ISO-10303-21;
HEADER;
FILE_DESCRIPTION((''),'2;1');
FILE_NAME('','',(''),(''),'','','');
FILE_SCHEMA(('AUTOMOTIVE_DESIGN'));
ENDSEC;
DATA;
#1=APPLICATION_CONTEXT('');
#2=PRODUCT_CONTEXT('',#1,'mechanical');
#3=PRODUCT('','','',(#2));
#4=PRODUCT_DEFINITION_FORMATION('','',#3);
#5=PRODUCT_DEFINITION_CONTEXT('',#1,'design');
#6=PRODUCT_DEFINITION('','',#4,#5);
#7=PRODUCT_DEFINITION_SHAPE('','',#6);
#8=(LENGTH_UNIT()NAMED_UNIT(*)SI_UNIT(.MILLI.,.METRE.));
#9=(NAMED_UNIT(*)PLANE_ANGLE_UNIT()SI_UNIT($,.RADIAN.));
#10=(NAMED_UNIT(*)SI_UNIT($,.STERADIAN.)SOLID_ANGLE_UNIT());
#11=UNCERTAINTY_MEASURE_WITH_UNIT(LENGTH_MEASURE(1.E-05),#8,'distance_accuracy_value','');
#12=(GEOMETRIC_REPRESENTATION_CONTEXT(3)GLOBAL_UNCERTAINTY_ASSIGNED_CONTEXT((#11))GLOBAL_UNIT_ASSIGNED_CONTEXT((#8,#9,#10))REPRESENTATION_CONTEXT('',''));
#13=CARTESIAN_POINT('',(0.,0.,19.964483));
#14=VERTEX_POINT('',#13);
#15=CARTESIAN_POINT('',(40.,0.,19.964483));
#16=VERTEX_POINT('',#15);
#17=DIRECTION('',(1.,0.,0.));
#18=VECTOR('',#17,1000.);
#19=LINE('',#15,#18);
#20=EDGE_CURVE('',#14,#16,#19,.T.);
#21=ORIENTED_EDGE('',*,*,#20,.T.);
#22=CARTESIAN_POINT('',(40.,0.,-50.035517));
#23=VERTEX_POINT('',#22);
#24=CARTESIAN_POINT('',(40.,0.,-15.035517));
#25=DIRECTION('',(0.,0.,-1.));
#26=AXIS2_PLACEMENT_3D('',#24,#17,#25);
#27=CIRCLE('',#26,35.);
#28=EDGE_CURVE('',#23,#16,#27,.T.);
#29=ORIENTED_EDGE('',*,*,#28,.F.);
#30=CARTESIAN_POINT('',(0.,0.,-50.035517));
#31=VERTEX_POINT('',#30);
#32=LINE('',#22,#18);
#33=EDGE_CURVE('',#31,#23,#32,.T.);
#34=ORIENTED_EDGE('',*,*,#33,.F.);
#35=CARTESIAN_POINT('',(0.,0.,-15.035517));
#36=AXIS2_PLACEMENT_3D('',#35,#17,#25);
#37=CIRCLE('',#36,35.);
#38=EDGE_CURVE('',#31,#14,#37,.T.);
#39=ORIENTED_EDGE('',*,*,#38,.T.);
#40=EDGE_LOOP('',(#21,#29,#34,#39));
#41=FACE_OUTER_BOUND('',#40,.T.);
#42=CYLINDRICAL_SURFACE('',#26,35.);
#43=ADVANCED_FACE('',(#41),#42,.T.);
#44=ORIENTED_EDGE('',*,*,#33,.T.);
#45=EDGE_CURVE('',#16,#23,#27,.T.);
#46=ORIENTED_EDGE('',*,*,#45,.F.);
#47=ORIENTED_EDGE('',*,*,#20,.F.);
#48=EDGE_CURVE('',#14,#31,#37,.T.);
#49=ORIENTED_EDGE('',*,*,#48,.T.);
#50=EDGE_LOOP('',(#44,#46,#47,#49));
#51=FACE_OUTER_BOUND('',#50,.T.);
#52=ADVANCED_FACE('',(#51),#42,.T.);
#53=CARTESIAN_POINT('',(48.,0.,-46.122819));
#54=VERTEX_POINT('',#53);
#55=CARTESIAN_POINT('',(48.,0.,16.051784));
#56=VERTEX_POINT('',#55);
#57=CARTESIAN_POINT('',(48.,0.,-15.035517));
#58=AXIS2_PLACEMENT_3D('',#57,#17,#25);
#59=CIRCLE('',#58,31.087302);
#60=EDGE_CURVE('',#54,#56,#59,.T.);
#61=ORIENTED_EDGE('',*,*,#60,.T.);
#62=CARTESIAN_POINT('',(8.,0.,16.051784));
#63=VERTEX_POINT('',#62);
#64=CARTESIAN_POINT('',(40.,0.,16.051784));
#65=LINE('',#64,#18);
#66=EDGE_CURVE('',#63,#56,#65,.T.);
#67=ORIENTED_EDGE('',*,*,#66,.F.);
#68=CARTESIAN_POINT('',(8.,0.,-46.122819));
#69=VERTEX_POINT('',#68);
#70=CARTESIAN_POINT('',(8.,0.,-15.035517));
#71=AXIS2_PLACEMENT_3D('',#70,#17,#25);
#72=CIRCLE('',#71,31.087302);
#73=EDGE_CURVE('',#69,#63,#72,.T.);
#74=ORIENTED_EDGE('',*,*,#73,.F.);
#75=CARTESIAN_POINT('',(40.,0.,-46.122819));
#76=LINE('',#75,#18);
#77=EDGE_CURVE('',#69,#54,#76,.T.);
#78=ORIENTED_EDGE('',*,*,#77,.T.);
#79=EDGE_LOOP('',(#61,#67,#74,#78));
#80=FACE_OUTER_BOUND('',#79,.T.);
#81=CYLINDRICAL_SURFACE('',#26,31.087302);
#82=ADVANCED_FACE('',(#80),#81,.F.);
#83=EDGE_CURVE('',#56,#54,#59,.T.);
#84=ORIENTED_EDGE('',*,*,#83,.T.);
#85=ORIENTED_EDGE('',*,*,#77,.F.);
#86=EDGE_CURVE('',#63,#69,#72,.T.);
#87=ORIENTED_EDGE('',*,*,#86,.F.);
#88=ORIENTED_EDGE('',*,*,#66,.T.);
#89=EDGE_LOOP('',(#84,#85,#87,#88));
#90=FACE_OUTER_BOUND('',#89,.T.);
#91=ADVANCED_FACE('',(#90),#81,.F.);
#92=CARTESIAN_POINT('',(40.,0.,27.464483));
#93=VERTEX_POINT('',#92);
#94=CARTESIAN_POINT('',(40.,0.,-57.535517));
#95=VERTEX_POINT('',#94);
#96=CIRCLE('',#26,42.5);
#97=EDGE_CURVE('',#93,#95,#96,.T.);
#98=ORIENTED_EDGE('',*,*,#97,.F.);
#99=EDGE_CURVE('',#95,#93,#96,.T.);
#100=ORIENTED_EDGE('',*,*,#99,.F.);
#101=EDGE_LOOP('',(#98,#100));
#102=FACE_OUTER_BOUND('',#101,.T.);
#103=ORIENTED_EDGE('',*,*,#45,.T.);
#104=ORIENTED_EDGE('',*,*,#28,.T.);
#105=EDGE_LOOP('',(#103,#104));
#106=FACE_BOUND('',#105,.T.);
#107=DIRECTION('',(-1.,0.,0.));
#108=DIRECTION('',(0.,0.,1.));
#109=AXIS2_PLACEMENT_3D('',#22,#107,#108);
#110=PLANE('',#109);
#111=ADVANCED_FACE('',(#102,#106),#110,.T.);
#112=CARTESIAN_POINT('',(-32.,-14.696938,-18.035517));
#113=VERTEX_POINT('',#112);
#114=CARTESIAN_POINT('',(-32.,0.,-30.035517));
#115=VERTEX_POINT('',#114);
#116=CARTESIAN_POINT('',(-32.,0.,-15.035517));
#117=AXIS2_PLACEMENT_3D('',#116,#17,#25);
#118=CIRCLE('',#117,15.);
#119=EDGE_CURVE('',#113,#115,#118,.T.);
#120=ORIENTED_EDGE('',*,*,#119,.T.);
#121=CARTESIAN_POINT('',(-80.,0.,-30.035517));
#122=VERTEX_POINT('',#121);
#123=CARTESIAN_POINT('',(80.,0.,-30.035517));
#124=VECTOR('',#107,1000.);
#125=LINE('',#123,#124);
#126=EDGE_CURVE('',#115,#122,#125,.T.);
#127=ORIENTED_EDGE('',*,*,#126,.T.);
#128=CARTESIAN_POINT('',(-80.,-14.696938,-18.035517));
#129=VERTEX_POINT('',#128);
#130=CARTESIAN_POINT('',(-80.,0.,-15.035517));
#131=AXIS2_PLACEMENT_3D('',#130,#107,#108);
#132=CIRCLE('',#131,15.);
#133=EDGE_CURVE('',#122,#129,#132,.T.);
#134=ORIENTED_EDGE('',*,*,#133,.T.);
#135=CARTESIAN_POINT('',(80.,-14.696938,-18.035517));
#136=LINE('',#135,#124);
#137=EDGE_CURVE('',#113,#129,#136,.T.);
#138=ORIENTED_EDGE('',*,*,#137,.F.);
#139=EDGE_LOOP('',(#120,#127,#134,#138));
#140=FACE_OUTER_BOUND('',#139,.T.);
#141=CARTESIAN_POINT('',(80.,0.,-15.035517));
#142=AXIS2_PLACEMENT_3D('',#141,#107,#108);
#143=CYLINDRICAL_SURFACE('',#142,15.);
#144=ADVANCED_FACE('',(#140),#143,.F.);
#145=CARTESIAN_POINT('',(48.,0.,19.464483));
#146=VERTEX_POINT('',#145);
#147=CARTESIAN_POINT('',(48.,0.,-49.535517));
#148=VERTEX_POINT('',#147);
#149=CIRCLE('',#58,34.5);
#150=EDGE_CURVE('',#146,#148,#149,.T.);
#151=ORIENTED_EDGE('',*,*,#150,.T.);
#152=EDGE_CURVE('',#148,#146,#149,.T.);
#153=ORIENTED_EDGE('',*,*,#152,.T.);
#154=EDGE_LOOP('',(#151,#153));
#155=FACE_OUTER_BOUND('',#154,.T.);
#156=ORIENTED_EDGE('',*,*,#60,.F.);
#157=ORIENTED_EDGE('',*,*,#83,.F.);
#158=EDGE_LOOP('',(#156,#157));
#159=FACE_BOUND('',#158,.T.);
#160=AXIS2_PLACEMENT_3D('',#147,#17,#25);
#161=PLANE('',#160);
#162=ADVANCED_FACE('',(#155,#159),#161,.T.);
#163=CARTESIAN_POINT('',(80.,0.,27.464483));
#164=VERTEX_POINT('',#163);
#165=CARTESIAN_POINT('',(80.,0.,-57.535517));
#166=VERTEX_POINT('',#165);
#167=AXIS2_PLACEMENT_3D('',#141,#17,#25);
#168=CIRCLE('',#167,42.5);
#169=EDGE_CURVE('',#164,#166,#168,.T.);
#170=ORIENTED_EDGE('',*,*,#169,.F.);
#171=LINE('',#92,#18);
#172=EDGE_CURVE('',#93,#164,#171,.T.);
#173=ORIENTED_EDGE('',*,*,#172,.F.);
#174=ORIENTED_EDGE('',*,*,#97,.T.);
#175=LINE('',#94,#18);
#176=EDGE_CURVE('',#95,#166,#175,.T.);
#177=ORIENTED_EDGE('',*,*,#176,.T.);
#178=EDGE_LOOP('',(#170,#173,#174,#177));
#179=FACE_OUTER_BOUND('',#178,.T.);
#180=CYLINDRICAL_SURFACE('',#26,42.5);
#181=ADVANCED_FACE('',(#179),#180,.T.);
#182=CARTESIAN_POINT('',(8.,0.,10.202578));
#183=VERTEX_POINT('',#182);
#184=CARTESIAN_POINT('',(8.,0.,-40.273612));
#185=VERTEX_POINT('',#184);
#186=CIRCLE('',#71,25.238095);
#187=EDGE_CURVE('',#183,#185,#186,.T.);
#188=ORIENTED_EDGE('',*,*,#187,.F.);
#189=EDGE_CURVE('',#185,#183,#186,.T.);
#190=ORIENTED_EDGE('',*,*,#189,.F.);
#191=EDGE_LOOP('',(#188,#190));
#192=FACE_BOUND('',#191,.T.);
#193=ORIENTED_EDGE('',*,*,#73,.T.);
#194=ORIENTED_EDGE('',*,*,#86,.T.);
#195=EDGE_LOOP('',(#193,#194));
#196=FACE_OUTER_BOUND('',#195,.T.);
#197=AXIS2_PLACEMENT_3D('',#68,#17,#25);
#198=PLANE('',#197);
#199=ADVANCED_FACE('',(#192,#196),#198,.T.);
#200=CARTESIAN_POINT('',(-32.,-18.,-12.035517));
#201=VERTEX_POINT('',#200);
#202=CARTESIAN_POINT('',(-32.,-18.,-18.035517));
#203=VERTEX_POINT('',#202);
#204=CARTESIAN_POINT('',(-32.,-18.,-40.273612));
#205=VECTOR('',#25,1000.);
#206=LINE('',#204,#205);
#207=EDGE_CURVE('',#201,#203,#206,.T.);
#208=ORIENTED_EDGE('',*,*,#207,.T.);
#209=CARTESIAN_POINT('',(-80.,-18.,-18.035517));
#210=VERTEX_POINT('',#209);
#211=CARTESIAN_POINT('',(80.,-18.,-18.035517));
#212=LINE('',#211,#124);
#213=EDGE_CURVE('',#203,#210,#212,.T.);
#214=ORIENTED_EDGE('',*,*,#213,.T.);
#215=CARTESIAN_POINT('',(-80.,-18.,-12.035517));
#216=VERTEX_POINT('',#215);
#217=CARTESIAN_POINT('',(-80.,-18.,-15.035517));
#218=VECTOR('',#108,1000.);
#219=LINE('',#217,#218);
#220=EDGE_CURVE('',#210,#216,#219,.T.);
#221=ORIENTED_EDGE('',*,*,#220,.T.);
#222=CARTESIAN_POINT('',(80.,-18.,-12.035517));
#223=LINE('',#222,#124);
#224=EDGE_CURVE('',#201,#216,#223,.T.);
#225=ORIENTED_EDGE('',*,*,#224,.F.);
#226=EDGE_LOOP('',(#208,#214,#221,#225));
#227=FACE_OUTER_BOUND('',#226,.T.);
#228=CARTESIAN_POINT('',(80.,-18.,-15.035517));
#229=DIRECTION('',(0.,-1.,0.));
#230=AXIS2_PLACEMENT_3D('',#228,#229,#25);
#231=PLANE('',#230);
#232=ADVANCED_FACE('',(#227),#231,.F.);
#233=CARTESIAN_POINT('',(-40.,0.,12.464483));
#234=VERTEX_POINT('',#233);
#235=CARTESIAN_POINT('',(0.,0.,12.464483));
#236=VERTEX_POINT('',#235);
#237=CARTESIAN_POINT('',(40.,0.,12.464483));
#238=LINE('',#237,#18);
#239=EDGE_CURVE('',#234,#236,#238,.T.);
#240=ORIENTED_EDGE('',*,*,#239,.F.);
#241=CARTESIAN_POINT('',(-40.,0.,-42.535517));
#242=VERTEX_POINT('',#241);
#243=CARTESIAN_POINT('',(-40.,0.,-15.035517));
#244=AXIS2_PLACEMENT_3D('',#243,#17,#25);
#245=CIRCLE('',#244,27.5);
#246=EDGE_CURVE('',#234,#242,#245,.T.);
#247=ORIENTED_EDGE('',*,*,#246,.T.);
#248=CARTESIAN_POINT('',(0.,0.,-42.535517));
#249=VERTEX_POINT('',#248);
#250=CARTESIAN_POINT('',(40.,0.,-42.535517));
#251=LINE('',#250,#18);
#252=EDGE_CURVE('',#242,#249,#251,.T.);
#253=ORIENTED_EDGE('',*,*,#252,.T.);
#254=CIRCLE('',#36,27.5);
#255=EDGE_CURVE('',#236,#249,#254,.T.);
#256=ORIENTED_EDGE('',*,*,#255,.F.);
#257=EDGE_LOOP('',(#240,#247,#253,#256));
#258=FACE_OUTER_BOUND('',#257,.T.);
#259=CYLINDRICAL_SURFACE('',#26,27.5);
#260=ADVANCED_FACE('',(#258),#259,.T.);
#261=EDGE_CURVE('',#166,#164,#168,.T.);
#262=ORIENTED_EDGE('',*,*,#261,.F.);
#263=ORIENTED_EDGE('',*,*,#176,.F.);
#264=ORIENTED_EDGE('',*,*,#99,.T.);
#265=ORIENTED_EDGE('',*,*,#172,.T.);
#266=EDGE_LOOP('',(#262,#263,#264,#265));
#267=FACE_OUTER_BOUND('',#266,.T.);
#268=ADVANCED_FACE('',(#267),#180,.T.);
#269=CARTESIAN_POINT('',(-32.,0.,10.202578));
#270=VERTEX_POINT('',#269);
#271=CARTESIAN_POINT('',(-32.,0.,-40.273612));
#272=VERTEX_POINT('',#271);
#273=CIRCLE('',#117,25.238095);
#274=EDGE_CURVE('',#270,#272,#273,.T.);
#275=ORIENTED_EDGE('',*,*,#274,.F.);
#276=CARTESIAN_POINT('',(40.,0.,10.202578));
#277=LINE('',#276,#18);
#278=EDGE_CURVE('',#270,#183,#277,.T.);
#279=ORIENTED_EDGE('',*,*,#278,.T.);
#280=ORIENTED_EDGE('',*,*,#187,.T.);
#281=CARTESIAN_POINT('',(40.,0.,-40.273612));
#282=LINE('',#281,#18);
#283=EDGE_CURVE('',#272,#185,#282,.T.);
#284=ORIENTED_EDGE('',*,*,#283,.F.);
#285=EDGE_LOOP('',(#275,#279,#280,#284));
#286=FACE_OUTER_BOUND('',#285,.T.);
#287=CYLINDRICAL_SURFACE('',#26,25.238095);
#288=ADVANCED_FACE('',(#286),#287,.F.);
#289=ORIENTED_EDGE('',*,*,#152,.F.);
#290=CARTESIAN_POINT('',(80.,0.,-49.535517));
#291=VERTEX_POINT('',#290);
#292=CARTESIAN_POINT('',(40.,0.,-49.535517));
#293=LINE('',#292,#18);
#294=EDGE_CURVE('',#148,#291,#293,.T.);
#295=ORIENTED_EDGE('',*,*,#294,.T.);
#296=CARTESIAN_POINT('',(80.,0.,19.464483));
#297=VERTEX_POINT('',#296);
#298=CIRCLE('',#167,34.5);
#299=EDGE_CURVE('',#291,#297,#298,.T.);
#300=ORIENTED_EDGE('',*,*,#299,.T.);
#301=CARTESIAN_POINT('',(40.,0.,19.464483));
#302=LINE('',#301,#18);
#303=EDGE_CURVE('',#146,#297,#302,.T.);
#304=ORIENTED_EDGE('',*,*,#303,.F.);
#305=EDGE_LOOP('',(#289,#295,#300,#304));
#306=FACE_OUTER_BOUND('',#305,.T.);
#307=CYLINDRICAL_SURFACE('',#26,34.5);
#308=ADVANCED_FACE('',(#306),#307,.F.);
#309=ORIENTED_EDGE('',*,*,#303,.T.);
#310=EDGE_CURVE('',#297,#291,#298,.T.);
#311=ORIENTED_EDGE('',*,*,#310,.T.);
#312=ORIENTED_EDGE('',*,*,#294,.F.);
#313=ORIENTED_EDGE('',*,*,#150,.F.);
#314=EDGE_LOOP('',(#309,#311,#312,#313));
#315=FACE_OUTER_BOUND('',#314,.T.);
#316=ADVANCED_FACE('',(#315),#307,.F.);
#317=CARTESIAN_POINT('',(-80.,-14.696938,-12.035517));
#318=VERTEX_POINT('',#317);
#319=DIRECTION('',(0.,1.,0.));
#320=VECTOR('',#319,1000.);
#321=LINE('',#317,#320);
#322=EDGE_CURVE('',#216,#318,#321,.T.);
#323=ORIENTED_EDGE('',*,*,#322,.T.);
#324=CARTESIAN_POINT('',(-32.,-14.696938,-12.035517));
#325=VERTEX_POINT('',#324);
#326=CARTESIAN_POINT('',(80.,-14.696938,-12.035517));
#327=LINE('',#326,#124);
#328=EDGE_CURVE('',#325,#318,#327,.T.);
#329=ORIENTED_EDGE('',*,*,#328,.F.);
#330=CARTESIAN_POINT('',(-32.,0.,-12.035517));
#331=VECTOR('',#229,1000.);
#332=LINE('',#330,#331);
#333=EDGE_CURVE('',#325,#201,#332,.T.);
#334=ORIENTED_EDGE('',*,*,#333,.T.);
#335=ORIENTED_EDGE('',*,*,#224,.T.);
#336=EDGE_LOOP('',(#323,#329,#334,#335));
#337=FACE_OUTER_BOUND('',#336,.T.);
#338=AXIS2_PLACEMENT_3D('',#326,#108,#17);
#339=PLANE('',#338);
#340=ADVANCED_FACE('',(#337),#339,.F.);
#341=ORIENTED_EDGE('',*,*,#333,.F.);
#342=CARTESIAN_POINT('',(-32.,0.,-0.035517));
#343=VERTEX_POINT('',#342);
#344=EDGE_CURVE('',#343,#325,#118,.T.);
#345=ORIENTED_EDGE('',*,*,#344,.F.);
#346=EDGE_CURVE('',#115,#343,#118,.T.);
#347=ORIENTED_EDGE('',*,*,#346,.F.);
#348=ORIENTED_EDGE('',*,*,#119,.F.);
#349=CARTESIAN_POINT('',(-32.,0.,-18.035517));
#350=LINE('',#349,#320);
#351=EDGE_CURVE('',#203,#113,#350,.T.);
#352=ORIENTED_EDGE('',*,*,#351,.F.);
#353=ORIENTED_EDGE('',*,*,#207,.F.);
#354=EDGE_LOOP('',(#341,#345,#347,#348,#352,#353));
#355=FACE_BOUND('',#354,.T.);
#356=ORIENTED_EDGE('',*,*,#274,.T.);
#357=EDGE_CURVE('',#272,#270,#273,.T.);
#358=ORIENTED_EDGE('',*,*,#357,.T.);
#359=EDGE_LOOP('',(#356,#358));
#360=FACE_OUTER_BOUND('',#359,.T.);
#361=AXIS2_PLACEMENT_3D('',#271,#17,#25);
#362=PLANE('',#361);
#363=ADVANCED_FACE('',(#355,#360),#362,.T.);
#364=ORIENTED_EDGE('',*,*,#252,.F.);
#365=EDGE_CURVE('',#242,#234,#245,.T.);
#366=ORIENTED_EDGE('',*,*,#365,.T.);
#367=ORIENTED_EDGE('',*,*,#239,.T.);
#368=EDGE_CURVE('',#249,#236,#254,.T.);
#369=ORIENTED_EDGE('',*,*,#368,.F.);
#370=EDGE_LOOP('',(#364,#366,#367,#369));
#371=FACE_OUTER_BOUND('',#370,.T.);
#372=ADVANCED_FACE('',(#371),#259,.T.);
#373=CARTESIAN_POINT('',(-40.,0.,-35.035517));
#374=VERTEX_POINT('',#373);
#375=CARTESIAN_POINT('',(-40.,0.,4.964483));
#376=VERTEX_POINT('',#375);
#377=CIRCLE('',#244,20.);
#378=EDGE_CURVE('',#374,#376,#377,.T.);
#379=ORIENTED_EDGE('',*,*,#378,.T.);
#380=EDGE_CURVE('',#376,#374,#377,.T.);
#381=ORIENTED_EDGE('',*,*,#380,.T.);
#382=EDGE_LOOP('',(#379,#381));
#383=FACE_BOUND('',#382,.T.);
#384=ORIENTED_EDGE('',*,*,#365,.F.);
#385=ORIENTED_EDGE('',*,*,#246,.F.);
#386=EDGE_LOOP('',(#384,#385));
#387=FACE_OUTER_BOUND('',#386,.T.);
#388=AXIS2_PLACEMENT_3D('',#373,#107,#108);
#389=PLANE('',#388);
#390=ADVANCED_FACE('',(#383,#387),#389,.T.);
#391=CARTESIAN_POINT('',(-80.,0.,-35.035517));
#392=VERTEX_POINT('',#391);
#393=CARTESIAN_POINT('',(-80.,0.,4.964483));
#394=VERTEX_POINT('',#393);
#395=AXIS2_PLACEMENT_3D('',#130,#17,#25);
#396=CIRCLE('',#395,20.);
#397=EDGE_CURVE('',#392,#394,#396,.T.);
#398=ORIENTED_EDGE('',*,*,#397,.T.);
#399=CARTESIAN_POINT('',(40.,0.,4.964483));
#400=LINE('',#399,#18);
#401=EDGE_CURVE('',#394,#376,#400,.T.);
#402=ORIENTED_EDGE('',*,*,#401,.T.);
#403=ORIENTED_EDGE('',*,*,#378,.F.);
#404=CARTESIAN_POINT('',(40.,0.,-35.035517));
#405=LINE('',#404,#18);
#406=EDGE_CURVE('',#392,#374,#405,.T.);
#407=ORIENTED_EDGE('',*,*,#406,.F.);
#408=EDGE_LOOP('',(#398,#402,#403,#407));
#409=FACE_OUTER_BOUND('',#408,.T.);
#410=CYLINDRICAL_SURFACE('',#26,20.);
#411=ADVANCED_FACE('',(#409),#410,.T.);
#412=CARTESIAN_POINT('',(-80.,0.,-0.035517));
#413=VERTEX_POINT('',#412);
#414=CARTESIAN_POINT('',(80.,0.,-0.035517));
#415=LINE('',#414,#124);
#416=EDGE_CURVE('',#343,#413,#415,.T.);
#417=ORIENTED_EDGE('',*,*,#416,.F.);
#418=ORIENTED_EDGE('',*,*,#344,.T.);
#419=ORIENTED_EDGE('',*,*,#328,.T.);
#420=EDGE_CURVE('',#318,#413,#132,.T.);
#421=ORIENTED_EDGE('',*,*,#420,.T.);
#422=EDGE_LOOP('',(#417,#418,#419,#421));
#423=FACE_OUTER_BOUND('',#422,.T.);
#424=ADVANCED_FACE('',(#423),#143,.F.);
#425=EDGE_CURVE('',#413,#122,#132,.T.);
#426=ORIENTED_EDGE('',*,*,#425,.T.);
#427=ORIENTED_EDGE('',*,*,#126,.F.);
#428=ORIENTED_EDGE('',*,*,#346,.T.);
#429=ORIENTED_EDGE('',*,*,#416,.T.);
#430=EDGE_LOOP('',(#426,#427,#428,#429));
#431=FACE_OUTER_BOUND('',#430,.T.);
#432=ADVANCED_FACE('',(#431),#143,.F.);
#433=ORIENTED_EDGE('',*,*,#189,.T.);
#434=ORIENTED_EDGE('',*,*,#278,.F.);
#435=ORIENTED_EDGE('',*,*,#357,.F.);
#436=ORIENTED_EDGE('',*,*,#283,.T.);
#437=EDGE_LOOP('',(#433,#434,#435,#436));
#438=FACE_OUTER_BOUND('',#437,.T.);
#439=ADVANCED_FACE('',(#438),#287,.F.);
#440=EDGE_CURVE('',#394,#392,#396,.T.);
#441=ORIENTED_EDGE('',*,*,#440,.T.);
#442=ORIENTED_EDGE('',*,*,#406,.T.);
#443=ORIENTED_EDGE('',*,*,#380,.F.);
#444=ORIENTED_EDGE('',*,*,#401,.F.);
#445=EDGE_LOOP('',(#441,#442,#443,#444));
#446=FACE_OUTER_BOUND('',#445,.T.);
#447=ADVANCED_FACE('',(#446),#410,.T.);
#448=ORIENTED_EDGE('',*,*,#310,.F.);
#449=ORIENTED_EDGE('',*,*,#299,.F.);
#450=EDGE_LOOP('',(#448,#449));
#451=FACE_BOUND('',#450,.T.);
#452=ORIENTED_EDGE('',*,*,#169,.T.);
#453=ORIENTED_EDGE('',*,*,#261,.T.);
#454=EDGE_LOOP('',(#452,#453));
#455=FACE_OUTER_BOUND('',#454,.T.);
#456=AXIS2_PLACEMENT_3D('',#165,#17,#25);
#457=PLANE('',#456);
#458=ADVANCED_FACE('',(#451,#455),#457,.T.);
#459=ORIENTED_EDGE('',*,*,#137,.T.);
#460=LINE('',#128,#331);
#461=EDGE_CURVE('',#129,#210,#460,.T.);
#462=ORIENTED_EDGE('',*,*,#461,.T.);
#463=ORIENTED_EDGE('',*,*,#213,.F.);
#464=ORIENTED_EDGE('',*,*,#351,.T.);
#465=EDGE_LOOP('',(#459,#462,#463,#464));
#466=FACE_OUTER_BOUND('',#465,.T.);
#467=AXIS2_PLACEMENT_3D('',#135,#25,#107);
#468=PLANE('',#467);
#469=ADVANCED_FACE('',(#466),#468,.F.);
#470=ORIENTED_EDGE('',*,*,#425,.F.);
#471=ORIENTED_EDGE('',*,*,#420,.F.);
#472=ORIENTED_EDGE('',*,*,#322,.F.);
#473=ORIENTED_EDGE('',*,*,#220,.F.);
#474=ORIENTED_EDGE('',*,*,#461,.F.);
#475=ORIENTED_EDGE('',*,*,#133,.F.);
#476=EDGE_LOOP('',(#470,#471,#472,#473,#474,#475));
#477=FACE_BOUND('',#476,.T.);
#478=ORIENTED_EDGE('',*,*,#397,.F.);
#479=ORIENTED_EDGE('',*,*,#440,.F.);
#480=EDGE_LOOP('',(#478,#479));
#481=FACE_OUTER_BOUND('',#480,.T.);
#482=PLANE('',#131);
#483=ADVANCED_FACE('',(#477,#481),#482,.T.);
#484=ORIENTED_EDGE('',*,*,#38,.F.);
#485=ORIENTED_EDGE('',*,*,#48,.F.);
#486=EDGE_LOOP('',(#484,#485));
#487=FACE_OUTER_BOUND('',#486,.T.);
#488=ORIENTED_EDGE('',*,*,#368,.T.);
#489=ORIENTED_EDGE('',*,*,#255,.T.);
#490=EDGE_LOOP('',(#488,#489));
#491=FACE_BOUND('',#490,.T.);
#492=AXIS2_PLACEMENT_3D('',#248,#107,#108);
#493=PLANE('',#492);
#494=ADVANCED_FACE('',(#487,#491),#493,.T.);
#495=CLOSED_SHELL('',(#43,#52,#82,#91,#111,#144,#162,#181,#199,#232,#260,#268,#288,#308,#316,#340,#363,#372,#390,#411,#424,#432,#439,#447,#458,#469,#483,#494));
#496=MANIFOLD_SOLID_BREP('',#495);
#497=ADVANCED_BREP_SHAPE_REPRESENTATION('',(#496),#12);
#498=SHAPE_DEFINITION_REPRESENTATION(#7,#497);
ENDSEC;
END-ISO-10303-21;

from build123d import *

# Parameters (mm, degrees)
END_BORE_30_DEEP_DEPTH = 176.261478164


with BuildPart() as part:
    # Stepped Profile Sketch → Stepped Pulley Body (revolve)
    with BuildSketch(Plane(origin=(0, 0, 0), x_dir=(1, 0, 0), z_dir=(0, 1, 0))):
        Polygon((-80, 15.035517104), (-80, 35.035517104), (-40, 35.035517104), (-40, 42.535517104), (0, 42.535517104), (0, 50.035517104), (40, 50.035517104), (40, 57.535517104), (80, 57.535517104), (80, 49.535517104), (48, 49.535517104), (48, 46.122818691), (8, 46.122818691), (8, 40.273612342), (-32, 40.273612342), (-32, 24.083136151), (40, 24.083136151), (40, 15.035517104), align=None)
    revolve(axis=Axis((40, 0, -15.035517104), (-1, 0, 0)))

    # End Bore Sketch → End Bore 30 Deep (cut, through all)
    with BuildSketch(Plane.ZY.offset(80)):
        with BuildLine():
            Line((-15.035517104, -18), (-12.035517104, -18))
            Line((-12.035517104, -18), (-12.035517104, -14.696938457))
            ThreePointArc((-12.035517104, -14.696938457), (-15.035517104, 15), (-18.035517104, -14.696938457))
            Line((-18.035517104, -14.696938457), (-18.035517104, -18))
            Line((-18.035517104, -18), (-15.035517104, -18))
        make_face()
    extrude(amount=-END_BORE_30_DEEP_DEPTH, mode=Mode.SUBTRACT)


solid = part.part
